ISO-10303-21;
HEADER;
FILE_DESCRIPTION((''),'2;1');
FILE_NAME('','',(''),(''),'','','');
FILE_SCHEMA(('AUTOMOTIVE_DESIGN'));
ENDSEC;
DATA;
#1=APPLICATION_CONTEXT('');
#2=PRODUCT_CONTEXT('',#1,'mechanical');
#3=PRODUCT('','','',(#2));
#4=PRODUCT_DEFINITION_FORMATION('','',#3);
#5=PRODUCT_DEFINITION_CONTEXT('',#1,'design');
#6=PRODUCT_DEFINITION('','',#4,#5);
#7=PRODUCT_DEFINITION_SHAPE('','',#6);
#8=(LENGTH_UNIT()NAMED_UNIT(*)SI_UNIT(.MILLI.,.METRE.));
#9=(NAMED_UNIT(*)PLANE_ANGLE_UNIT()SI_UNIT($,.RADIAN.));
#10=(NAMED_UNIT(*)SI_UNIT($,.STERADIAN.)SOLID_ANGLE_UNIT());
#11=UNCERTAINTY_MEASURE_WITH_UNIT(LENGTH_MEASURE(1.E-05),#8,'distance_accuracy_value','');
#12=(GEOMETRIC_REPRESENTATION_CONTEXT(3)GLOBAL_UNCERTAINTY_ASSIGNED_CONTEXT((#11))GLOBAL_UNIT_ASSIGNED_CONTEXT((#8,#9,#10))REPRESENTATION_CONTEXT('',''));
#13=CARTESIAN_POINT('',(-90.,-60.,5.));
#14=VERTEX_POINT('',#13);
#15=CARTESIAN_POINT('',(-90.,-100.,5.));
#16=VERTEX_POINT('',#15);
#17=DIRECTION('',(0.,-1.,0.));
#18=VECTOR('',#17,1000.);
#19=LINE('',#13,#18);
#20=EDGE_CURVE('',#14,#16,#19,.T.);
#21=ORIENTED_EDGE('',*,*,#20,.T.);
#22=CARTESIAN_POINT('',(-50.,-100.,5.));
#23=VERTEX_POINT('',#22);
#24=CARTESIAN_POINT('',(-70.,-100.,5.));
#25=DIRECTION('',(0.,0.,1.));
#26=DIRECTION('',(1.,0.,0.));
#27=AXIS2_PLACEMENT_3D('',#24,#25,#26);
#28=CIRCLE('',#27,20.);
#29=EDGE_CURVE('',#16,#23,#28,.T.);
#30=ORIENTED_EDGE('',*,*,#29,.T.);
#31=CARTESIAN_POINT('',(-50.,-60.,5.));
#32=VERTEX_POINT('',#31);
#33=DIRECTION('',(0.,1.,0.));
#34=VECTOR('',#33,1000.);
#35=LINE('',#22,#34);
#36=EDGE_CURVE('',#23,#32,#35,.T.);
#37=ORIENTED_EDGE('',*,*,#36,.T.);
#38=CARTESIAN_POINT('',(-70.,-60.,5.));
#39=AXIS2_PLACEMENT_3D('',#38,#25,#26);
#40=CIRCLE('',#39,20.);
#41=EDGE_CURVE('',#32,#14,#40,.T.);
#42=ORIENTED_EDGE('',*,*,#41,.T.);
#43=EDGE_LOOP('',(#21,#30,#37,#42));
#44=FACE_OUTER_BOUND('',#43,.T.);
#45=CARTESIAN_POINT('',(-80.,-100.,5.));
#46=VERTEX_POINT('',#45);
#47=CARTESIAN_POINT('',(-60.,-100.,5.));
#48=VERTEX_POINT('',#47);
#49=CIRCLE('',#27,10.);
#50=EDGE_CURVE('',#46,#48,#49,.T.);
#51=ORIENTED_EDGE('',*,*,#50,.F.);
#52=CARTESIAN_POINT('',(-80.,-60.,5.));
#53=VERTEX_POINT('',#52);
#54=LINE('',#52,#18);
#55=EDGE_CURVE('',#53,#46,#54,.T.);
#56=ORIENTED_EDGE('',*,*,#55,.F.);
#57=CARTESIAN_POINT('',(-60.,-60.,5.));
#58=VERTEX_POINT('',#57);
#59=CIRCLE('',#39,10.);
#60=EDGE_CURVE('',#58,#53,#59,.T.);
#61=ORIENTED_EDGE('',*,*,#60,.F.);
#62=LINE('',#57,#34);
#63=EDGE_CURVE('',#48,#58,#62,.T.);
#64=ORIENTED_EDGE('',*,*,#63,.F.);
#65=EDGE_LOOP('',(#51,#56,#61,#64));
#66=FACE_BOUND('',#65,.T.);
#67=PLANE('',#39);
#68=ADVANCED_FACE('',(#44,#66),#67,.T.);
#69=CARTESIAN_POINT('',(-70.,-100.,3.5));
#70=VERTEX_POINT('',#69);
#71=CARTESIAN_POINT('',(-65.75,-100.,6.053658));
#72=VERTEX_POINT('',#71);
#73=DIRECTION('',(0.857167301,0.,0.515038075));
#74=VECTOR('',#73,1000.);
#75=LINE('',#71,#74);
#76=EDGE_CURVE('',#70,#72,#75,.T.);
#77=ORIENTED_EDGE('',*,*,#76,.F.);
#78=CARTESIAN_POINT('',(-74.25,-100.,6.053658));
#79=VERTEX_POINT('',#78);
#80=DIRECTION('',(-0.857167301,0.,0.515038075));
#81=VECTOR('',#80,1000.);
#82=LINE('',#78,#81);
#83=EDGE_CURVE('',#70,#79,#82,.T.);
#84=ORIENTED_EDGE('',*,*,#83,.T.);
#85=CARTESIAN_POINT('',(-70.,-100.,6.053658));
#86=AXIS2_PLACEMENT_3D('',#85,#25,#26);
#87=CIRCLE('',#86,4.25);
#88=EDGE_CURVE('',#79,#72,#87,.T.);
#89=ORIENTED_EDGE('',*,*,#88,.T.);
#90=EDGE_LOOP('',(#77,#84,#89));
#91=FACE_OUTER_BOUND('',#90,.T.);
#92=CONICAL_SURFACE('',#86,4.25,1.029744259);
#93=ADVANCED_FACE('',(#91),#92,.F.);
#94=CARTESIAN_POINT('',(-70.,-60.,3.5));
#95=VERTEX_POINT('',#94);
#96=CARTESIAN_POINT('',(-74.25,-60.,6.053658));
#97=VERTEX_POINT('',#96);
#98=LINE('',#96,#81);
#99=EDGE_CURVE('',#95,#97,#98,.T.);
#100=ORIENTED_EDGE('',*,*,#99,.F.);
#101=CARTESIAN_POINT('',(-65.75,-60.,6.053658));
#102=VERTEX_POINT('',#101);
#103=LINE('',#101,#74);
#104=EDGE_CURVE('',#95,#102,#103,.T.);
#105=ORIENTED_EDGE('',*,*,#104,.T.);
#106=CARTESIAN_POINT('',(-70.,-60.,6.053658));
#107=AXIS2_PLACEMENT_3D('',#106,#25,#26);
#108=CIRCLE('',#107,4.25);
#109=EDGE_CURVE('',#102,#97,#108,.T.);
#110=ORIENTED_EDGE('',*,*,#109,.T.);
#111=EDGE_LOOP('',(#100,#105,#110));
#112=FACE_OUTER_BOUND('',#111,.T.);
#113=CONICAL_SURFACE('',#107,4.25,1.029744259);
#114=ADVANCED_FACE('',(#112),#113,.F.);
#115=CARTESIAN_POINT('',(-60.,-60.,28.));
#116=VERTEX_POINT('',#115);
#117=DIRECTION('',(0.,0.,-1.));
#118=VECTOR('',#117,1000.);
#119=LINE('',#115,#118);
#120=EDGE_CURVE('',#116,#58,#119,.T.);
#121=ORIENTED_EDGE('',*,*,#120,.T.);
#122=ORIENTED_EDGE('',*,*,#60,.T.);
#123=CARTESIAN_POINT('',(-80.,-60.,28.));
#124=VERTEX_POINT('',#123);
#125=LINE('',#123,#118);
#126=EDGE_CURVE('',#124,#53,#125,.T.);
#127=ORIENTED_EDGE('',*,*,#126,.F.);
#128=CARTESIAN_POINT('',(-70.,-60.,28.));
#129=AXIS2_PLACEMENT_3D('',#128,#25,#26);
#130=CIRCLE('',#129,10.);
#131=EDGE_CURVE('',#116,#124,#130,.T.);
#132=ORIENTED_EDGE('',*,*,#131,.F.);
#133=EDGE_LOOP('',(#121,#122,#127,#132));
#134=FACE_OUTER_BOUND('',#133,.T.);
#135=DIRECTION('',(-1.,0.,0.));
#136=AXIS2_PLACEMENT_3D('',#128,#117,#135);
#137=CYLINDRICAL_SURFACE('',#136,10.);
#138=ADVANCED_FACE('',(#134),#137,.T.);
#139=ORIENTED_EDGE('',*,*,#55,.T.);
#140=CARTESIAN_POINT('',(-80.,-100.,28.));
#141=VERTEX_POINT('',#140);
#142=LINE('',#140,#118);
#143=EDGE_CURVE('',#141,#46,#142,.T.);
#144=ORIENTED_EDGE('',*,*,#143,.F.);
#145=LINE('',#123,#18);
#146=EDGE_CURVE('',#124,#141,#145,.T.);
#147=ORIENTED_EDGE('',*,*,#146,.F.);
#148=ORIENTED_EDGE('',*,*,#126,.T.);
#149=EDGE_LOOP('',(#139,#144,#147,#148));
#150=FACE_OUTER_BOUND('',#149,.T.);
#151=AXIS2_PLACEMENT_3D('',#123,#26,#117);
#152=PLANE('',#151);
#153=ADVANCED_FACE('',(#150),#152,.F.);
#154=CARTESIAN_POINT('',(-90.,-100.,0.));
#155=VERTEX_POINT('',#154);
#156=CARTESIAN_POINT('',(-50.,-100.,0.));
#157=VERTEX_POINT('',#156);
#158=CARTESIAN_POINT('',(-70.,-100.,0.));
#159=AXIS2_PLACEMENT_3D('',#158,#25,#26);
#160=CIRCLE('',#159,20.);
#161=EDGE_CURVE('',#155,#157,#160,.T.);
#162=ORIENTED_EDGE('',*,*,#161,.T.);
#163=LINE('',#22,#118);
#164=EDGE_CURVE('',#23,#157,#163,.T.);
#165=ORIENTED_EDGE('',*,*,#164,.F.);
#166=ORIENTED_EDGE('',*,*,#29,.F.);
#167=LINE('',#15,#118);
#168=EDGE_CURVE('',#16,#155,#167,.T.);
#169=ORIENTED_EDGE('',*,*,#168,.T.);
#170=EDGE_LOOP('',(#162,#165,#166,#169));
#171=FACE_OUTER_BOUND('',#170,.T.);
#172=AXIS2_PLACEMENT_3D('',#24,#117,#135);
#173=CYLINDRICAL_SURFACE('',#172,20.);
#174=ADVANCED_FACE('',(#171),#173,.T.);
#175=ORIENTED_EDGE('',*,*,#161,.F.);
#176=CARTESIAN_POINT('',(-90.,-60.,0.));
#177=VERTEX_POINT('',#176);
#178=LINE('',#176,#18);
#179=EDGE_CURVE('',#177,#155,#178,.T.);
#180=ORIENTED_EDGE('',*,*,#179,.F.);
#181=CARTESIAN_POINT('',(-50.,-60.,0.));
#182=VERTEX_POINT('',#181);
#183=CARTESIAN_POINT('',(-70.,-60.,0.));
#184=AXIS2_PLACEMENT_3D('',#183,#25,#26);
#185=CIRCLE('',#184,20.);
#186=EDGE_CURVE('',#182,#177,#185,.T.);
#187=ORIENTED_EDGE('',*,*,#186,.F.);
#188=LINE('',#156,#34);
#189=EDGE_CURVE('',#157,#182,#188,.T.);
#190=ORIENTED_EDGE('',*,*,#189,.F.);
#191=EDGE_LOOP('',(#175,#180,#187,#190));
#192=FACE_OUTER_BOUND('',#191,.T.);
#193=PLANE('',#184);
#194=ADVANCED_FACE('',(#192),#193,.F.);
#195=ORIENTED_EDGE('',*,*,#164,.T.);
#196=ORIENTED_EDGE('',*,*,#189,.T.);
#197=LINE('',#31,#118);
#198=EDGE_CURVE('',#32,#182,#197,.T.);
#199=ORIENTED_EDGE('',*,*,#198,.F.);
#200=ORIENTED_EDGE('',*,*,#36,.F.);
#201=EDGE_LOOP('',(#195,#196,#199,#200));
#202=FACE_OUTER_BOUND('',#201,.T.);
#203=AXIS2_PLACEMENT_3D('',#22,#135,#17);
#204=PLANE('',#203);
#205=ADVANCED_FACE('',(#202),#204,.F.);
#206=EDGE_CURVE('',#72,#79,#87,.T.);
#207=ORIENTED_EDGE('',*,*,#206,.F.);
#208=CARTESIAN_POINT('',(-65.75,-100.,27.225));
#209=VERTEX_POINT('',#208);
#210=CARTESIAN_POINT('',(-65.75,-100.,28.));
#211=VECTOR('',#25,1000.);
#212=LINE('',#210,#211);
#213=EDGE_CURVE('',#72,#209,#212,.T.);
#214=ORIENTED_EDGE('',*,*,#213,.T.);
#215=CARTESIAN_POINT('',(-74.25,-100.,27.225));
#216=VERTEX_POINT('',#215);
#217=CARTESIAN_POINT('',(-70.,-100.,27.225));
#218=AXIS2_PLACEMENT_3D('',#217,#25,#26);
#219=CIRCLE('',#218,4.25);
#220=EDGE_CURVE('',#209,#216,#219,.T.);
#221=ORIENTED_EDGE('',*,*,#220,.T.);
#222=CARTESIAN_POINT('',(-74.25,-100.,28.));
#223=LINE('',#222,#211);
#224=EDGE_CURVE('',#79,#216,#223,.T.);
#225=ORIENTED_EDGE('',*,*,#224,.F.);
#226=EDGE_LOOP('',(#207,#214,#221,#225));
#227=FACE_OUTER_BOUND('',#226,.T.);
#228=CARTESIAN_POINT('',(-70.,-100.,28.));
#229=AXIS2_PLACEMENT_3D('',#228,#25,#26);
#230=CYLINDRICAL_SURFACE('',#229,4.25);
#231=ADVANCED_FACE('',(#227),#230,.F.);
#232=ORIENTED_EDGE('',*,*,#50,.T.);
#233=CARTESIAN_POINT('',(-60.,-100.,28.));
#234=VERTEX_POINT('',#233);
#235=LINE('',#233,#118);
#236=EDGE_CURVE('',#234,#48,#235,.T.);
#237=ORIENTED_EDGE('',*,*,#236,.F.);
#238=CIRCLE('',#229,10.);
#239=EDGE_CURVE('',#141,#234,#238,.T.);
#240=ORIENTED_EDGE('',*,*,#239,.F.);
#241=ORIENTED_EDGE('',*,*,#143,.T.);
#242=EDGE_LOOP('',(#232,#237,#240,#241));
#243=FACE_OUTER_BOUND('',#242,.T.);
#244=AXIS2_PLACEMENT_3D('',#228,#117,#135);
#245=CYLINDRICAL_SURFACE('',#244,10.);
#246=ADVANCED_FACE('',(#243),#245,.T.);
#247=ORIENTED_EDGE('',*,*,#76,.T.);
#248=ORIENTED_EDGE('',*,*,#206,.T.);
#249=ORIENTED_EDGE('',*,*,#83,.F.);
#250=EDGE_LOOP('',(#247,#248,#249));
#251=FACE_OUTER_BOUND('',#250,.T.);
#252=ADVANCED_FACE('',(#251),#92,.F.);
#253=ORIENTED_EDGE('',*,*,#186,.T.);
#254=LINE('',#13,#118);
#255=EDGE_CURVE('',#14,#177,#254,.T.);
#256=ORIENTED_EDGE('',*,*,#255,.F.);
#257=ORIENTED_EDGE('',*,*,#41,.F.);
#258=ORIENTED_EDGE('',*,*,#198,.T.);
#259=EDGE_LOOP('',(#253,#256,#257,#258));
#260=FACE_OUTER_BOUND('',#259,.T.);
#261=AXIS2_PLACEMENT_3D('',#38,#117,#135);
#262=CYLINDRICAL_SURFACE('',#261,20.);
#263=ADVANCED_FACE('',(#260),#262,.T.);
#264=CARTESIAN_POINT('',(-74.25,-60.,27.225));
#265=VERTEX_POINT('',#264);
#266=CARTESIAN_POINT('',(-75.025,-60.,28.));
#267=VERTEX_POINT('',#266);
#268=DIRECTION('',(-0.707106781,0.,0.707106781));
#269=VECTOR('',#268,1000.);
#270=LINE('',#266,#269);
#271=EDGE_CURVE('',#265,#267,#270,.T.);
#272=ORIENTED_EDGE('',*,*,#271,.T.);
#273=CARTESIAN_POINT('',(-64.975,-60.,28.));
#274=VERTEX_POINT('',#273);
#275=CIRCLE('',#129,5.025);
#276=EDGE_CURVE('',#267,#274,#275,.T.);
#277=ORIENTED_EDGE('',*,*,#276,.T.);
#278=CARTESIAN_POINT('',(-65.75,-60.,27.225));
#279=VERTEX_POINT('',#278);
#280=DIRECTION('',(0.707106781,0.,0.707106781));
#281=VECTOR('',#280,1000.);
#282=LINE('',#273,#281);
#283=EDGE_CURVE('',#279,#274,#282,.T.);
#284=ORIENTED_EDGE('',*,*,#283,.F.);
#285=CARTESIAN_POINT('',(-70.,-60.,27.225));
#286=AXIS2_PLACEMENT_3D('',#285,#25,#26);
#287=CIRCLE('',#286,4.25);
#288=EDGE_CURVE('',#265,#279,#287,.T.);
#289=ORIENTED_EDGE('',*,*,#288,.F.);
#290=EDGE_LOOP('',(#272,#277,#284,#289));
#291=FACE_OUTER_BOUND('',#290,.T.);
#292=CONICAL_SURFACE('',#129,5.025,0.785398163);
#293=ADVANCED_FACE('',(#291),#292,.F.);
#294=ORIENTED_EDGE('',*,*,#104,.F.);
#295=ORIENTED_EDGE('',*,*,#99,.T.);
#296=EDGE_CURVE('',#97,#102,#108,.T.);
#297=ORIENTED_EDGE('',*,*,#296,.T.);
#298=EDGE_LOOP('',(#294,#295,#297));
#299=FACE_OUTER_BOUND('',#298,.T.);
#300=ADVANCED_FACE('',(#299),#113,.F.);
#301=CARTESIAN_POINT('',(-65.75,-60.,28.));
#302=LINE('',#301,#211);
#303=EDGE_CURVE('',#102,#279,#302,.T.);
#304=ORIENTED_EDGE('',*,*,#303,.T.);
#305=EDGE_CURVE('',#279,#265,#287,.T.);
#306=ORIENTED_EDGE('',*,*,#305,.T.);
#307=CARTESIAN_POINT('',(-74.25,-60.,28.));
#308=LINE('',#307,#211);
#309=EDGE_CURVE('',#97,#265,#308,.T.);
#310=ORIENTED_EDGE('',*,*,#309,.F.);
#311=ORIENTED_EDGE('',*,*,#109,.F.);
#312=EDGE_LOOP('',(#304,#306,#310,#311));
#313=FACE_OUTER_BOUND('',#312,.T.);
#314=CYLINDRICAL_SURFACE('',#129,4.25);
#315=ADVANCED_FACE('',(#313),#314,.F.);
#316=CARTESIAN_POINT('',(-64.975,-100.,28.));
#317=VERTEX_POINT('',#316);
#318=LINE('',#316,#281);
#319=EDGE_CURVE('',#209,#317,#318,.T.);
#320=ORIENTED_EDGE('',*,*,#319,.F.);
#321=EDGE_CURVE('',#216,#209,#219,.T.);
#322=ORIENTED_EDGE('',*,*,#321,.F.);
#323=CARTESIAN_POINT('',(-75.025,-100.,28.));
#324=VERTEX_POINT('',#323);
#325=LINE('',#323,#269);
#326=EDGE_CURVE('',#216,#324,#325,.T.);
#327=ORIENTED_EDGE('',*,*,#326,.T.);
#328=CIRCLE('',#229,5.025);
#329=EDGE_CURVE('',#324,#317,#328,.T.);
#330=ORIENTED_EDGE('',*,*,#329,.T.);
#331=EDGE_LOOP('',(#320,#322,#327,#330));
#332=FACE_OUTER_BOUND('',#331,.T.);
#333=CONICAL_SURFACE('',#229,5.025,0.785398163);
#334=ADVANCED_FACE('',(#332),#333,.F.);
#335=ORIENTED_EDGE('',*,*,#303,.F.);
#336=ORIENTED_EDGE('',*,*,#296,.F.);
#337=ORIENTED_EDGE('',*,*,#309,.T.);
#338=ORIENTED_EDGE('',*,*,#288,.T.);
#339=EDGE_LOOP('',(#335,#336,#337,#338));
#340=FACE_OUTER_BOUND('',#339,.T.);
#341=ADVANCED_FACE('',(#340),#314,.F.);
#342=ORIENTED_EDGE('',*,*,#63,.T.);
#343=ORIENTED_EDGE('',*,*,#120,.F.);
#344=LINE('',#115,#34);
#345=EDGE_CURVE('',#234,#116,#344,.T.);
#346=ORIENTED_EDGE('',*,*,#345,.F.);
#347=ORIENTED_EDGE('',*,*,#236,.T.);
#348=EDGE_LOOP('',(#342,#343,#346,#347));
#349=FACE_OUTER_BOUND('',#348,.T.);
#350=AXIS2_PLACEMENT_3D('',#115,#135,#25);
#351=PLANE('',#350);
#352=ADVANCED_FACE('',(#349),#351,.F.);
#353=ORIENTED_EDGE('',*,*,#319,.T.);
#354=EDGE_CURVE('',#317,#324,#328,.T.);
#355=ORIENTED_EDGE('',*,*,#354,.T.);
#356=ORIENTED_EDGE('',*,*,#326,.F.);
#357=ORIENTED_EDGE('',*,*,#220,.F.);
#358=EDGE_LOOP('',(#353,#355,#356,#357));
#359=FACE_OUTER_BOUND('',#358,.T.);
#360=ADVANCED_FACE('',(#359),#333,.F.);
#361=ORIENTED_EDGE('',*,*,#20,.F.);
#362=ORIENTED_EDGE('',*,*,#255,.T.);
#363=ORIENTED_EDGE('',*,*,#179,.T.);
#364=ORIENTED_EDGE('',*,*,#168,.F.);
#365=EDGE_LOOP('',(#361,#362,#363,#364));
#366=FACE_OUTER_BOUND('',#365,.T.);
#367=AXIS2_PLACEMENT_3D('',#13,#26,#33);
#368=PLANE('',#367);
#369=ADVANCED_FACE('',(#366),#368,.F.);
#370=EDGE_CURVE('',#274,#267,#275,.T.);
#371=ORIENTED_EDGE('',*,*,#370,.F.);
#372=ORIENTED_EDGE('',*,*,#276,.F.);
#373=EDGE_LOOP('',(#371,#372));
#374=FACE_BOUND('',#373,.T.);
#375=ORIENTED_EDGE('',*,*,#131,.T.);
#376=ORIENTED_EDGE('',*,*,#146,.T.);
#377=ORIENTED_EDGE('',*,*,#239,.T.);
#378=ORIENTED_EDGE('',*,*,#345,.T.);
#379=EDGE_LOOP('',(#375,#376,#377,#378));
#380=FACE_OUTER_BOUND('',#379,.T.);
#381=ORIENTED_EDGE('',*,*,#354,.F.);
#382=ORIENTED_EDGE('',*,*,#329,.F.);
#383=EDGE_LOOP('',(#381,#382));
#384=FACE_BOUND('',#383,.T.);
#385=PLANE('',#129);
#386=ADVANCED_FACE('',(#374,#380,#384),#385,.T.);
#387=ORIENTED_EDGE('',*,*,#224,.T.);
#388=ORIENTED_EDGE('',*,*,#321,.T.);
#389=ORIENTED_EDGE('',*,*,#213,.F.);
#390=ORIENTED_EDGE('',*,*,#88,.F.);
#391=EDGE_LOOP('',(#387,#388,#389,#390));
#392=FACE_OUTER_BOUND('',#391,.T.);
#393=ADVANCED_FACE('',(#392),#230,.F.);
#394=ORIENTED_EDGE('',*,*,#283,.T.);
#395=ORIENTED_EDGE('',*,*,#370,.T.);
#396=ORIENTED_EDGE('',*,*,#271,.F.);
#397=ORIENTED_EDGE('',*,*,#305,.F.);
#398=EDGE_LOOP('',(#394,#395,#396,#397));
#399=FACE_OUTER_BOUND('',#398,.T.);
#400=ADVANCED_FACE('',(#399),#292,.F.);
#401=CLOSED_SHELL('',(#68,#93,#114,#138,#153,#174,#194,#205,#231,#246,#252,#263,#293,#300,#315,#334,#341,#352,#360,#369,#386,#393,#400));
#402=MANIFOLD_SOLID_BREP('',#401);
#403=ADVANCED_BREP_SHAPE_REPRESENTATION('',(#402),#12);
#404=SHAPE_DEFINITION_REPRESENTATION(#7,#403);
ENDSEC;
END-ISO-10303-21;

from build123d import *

# Parameters (mm, degrees)
EXTRUDE_1_DEPTH               = 28
EXTRUDE_2_DEPTH               = 5
HOLE_WIZARD_M10_1_D           = 8.5
HOLE_WIZARD_M10_1_DEPTH       = 21.946342369
HOLE_WIZARD_M10_1_CSINK_D     = 10.05
HOLE_WIZARD_M10_1_CSINK_ANGLE = 90
HOLE_WIZARD_M10_1_TIP         = 2.553657631


with BuildPart() as part:
    # 草图1 → 凸台-拉伸1 (new body)
    with BuildSketch(Plane.XY):
        with BuildLine():
            Line((-60, -60), (-60, -100))
            ThreePointArc((-60, -100), (-70, -110), (-80, -100))
            Line((-80, -100), (-80, -60))
            ThreePointArc((-80, -60), (-70, -50), (-60, -60))
        make_face()
    extrude(amount=EXTRUDE_1_DEPTH)

    # 草图2 → 凸台-拉伸2 (add)
    with BuildSketch(Plane.XY):
        with BuildLine():
            Line((-90, -60), (-90, -100))
            ThreePointArc((-90, -100), (-70, -120), (-50, -100))
            Line((-50, -100), (-50, -60))
            ThreePointArc((-50, -60), (-70, -40), (-90, -60))
        make_face()
    extrude(amount=EXTRUDE_2_DEPTH)

    # M10 螺纹孔1
    with Locations(Plane.XY.offset(28)):
        with Locations((-70, -60), (-70, -100)):
            CounterSinkHole(HOLE_WIZARD_M10_1_D / 2, HOLE_WIZARD_M10_1_CSINK_D / 2, depth=HOLE_WIZARD_M10_1_DEPTH, counter_sink_angle=HOLE_WIZARD_M10_1_CSINK_ANGLE)
            with Locations((0, 0, -(HOLE_WIZARD_M10_1_DEPTH + HOLE_WIZARD_M10_1_TIP / 2))):  # 118° drill point
                Cone(0, HOLE_WIZARD_M10_1_D / 2, HOLE_WIZARD_M10_1_TIP, mode=Mode.SUBTRACT)


solid = part.part
